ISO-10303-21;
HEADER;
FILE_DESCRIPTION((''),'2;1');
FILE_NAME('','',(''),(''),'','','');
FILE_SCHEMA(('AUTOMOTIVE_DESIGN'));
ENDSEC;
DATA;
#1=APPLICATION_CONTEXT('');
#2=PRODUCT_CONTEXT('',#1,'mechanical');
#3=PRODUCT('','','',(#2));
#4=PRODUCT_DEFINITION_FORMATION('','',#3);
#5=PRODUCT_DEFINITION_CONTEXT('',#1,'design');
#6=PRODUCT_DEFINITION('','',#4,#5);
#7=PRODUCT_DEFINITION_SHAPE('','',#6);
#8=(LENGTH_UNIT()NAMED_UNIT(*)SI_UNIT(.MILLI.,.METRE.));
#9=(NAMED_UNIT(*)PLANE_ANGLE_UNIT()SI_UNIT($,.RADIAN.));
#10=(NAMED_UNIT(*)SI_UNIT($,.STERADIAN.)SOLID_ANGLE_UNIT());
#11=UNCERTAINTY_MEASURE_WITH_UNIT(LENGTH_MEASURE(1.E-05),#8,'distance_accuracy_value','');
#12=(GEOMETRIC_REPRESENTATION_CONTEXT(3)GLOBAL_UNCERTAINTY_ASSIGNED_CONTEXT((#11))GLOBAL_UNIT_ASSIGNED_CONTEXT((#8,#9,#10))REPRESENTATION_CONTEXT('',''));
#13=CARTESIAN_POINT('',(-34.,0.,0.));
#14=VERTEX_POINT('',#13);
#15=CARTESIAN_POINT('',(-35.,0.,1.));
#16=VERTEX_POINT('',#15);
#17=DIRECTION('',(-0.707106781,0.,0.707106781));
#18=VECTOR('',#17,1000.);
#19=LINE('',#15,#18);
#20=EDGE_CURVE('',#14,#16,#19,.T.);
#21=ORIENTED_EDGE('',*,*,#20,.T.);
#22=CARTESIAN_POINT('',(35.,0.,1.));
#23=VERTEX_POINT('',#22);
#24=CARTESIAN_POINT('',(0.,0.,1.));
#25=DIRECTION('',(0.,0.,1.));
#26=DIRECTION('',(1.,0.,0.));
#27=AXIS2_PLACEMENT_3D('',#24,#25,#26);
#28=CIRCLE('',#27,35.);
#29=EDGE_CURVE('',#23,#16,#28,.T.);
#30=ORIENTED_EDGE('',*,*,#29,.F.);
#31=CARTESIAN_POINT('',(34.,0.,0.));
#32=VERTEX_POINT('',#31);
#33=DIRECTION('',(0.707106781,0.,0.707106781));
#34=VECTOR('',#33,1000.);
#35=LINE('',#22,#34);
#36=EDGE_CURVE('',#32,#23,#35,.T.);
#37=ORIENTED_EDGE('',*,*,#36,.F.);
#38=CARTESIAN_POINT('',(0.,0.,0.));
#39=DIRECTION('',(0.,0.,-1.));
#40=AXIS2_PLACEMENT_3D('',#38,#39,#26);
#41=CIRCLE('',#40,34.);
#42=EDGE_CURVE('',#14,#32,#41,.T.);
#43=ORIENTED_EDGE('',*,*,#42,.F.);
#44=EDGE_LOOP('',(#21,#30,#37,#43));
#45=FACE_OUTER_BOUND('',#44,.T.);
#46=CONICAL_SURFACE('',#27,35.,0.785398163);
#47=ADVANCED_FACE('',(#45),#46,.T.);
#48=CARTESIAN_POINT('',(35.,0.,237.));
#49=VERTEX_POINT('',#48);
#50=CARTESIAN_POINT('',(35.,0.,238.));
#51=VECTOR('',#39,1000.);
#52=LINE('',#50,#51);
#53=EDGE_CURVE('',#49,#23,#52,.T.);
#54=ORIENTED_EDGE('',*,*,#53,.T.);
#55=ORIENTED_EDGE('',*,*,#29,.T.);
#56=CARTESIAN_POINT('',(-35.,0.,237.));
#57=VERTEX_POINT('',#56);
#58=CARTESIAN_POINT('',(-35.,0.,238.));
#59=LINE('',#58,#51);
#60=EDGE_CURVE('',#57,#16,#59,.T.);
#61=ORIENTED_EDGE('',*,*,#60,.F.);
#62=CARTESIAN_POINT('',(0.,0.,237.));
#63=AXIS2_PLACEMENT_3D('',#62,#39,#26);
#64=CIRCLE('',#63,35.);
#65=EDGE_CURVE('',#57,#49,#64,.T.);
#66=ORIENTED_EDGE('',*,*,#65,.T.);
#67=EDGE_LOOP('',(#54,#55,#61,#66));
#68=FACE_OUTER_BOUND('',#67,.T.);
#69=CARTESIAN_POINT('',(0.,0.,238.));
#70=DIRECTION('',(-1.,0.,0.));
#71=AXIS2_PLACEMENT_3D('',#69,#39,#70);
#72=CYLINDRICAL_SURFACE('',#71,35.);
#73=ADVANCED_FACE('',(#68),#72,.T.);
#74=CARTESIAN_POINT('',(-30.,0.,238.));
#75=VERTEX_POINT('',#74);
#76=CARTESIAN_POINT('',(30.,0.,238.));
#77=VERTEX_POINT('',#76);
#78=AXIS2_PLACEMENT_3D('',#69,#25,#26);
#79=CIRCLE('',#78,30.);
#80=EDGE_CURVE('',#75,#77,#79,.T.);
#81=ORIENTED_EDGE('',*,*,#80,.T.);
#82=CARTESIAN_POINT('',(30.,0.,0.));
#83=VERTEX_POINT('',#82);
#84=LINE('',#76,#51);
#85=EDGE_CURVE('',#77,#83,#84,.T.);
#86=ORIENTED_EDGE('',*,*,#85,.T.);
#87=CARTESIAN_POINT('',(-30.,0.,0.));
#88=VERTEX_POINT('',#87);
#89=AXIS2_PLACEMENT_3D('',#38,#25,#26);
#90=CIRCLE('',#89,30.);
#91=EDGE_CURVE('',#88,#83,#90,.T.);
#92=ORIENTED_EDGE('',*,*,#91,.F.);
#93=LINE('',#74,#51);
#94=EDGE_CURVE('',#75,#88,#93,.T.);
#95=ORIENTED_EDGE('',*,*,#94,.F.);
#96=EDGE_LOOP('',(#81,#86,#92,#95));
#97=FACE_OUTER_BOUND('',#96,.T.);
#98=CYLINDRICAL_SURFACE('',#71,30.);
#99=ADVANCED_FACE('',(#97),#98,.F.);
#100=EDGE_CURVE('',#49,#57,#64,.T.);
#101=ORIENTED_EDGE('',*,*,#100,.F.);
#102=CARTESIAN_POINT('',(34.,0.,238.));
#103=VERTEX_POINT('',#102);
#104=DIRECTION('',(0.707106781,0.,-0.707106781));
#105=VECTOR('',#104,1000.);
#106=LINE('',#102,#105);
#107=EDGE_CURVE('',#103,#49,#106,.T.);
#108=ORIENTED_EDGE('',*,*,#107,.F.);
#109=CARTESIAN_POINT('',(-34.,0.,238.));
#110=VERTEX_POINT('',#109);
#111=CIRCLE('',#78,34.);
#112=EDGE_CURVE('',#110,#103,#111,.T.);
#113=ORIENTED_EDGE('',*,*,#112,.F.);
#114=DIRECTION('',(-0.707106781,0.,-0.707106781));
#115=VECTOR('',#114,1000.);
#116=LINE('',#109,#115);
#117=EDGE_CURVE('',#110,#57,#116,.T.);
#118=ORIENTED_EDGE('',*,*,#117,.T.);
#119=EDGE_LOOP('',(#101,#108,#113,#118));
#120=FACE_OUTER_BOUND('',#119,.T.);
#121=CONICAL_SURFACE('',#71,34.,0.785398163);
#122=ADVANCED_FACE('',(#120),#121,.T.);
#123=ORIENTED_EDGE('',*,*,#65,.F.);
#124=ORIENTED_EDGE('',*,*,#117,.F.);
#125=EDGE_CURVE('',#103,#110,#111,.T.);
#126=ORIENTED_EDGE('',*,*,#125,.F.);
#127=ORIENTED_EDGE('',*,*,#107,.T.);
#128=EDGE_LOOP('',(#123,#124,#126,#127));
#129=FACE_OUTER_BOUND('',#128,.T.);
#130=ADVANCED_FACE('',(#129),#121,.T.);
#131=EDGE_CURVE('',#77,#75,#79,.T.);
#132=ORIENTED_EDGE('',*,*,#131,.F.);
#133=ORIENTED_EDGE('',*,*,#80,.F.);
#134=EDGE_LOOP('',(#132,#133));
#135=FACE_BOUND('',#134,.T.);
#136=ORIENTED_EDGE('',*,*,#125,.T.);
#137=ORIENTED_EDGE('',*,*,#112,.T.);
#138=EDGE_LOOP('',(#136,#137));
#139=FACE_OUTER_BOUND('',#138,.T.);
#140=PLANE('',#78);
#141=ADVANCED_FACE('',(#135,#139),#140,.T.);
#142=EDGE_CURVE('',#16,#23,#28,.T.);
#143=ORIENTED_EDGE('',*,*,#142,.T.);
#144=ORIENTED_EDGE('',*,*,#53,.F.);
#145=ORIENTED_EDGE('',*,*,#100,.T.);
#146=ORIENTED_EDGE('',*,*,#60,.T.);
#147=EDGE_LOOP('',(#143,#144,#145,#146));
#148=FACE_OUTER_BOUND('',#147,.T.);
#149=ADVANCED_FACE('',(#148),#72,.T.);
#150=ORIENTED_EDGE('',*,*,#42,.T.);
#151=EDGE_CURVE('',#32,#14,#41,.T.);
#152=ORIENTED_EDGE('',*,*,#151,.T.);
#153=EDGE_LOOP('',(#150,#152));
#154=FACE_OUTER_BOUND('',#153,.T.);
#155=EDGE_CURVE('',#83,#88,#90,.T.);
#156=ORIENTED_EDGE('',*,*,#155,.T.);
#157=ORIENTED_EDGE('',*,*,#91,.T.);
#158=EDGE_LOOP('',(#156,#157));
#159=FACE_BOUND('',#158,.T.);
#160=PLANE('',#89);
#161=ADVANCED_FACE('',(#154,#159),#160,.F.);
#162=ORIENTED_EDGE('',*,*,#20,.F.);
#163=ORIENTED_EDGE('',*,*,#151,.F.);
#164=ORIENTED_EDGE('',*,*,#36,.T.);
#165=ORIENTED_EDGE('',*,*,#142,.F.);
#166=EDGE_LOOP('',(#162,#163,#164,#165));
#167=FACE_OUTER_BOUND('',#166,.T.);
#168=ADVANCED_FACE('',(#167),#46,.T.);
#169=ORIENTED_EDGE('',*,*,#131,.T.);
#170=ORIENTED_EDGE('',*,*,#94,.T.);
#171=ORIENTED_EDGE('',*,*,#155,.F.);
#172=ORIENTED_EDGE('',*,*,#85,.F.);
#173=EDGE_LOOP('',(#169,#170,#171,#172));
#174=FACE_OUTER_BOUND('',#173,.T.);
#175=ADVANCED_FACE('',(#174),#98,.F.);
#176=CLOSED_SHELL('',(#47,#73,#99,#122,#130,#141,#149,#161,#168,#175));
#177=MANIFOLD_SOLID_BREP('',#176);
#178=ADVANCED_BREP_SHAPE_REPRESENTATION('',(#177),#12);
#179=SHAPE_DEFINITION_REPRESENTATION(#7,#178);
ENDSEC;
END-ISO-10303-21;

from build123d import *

# Parameters (mm, degrees)
SKETCH1_R           = 35
SKETCH1_R_2         = 30
BOSS_EXTRUDE1_DEPTH = 238
CHAMFER1_SIZE       = 1


with BuildPart() as part:
    # Sketch1 → Boss-Extrude1 (new body)
    with BuildSketch(Plane.XY):
        Circle(SKETCH1_R)
        Circle(SKETCH1_R_2, mode=Mode.SUBTRACT)
    extrude(amount=BOSS_EXTRUDE1_DEPTH)

    # Chamfer1
    chamfer1_edges = [part.edges().sort_by_distance(p)[0] for p in [
        (-35, 0, 0),
        (-35, 0, 238),
    ]]
    chamfer(chamfer1_edges, length=CHAMFER1_SIZE)


solid = part.part
